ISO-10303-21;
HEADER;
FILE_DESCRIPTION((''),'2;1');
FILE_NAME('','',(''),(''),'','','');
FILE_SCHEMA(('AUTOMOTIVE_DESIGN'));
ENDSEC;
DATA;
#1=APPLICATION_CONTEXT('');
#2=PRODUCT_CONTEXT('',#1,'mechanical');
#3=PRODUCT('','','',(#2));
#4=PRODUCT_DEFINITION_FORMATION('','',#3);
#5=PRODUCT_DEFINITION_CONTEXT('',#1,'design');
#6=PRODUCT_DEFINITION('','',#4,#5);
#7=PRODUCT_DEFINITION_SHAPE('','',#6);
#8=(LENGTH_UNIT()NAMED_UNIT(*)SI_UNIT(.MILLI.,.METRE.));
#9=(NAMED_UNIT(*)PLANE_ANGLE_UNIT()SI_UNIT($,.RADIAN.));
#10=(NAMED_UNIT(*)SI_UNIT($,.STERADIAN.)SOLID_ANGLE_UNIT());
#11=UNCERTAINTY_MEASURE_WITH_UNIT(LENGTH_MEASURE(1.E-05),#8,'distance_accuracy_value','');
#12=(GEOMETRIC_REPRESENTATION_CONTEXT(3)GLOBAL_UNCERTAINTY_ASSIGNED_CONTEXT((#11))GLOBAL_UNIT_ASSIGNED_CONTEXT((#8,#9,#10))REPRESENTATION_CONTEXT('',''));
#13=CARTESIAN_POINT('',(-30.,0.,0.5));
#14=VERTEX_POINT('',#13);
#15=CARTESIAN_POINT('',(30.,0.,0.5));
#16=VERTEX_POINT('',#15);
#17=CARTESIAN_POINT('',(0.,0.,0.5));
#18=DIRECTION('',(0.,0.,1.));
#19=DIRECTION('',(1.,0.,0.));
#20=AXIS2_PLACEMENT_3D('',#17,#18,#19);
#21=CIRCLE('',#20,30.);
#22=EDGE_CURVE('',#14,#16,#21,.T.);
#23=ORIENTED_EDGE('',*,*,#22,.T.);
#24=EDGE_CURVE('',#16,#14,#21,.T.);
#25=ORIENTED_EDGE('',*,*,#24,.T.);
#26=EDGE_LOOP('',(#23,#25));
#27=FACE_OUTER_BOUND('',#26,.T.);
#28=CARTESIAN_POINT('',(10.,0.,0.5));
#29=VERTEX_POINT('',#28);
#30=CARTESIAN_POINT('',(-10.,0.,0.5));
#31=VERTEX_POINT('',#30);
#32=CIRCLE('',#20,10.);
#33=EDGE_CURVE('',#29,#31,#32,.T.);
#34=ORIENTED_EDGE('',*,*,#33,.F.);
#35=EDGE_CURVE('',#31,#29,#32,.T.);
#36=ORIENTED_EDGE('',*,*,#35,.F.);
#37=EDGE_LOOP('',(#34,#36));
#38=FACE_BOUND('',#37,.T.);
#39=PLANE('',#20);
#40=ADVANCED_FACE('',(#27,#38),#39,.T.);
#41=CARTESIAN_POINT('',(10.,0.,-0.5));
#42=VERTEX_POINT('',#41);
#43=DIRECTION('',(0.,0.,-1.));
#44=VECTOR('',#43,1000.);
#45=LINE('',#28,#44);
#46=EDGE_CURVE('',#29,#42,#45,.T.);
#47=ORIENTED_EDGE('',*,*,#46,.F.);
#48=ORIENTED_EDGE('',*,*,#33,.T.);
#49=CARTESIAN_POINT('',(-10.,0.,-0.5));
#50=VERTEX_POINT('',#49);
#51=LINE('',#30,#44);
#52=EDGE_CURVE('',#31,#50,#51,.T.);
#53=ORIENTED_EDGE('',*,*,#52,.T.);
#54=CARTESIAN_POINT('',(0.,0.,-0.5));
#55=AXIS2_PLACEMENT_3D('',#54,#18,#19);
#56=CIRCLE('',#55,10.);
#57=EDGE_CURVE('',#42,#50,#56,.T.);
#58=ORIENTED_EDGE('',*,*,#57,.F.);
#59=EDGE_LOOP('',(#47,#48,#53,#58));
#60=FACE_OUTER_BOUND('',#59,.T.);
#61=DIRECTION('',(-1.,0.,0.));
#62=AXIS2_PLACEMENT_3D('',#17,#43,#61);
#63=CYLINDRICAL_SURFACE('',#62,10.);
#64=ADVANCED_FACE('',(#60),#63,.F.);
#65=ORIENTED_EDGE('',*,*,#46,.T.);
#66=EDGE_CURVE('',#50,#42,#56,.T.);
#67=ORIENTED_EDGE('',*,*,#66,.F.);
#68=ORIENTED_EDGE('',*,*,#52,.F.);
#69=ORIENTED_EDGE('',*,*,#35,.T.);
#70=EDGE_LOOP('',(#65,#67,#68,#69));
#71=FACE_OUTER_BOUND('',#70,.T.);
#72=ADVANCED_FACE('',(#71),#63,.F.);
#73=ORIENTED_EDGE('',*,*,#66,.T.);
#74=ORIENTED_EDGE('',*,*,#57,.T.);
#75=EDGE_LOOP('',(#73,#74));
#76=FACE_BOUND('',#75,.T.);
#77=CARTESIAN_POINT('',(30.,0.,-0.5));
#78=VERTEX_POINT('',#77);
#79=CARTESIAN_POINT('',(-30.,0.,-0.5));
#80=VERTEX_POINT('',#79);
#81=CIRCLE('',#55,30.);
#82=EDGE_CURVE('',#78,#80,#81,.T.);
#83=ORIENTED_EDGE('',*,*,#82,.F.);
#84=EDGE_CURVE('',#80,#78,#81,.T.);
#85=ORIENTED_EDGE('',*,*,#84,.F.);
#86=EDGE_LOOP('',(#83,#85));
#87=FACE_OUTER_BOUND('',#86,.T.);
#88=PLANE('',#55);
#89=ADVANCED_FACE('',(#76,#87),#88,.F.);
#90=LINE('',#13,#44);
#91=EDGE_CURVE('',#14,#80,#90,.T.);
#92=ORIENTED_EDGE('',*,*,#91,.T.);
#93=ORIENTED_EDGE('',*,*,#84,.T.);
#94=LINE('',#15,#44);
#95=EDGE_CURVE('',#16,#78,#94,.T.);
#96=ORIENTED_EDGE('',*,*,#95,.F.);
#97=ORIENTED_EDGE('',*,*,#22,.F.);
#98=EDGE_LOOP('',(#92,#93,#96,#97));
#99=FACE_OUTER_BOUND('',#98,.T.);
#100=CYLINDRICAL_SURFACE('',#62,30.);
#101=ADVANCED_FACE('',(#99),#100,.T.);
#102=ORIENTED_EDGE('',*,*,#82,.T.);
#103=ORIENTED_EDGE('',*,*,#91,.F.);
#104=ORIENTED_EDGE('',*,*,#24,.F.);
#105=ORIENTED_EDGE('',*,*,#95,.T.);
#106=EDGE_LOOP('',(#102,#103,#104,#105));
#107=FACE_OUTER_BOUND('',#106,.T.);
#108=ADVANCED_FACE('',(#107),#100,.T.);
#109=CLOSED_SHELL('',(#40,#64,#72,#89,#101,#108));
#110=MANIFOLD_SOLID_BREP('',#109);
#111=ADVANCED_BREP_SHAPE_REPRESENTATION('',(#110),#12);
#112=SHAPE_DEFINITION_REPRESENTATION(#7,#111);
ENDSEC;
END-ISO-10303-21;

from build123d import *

# Parameters (mm, degrees)
SKETCH1_R           = 30
SKETCH1_R_2         = 10
BOSS_EXTRUDE1_DEPTH = 0.5


with BuildPart() as part:
    # Sketch1 → Boss-Extrude1 (new, symmetric)
    with BuildSketch(Plane.XY):
        Circle(SKETCH1_R)
        Circle(SKETCH1_R_2, mode=Mode.SUBTRACT)
    extrude(amount=BOSS_EXTRUDE1_DEPTH, both=True)


solid = part.part
